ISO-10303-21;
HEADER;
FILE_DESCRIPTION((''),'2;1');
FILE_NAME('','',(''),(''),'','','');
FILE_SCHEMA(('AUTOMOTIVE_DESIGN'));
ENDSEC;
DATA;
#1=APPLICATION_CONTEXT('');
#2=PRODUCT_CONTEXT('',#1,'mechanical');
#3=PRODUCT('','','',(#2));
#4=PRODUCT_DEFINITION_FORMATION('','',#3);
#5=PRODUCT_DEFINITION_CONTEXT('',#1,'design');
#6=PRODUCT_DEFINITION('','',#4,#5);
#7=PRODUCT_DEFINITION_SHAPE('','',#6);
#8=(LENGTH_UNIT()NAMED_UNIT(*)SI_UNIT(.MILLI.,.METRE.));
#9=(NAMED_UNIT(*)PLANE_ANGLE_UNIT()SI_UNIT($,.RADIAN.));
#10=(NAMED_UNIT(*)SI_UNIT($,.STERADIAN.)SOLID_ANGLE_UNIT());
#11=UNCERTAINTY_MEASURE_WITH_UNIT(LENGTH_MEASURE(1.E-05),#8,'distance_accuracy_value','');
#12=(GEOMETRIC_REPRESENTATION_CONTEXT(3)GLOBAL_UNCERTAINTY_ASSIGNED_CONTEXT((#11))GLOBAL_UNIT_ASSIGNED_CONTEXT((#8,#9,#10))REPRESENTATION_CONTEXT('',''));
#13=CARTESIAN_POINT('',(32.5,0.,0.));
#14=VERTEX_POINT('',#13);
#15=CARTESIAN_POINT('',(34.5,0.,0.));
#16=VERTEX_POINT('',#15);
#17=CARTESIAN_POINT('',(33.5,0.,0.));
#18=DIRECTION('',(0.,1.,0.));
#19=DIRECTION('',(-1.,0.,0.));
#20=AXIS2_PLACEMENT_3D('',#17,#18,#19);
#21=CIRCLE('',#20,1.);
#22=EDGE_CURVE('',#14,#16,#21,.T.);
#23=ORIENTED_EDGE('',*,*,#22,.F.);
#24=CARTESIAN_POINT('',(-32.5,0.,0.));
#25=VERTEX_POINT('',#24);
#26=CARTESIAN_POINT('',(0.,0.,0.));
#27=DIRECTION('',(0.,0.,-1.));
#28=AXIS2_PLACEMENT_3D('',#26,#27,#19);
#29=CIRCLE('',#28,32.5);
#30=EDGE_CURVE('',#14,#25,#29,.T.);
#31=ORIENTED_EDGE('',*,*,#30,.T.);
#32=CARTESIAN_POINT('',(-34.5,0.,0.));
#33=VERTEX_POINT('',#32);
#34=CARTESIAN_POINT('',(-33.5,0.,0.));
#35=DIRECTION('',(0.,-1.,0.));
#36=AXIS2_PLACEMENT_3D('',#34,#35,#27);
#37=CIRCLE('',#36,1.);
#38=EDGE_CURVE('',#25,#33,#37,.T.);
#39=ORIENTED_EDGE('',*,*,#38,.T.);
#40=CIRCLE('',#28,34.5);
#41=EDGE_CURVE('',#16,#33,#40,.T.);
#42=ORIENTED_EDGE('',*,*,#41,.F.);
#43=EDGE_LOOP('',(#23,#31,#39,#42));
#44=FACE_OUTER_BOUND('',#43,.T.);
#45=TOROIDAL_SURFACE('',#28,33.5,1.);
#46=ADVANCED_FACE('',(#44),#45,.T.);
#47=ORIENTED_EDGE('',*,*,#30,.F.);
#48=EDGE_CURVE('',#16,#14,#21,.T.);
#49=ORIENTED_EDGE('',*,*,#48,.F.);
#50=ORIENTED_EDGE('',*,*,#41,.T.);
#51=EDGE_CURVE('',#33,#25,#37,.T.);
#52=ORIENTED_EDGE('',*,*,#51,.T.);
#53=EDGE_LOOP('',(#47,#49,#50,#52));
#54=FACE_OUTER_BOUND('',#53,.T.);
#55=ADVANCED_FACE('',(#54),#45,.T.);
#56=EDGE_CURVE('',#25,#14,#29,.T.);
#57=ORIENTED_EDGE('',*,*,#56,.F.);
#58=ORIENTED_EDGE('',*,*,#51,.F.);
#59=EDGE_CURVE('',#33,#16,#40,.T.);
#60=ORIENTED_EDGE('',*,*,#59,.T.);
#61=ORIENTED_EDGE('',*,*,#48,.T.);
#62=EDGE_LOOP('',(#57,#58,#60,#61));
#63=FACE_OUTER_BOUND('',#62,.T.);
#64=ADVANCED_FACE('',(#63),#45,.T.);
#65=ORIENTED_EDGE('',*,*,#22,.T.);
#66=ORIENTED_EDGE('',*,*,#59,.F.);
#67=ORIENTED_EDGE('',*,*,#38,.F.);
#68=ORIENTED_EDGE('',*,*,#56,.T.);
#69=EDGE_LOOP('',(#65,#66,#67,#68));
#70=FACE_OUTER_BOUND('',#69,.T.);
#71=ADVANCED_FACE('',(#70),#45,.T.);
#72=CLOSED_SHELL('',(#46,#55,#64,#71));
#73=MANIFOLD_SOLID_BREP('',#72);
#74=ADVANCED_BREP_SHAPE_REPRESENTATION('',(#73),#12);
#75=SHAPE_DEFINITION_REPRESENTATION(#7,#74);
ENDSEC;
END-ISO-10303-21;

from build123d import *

# Parameters (mm, degrees)
SKETCH1_R = 1


with BuildPart() as part:
    # Sketch1 → Revolve1 (revolve)
    with BuildSketch(Plane(origin=(0, 0, 0), x_dir=(1, 0, 0), z_dir=(0, 1, 0))):
        with Locations((-33.5, 0)):
            Circle(SKETCH1_R)
    revolve(axis=Axis((0, 0, 0), (0, 0, 1)))


solid = part.part
